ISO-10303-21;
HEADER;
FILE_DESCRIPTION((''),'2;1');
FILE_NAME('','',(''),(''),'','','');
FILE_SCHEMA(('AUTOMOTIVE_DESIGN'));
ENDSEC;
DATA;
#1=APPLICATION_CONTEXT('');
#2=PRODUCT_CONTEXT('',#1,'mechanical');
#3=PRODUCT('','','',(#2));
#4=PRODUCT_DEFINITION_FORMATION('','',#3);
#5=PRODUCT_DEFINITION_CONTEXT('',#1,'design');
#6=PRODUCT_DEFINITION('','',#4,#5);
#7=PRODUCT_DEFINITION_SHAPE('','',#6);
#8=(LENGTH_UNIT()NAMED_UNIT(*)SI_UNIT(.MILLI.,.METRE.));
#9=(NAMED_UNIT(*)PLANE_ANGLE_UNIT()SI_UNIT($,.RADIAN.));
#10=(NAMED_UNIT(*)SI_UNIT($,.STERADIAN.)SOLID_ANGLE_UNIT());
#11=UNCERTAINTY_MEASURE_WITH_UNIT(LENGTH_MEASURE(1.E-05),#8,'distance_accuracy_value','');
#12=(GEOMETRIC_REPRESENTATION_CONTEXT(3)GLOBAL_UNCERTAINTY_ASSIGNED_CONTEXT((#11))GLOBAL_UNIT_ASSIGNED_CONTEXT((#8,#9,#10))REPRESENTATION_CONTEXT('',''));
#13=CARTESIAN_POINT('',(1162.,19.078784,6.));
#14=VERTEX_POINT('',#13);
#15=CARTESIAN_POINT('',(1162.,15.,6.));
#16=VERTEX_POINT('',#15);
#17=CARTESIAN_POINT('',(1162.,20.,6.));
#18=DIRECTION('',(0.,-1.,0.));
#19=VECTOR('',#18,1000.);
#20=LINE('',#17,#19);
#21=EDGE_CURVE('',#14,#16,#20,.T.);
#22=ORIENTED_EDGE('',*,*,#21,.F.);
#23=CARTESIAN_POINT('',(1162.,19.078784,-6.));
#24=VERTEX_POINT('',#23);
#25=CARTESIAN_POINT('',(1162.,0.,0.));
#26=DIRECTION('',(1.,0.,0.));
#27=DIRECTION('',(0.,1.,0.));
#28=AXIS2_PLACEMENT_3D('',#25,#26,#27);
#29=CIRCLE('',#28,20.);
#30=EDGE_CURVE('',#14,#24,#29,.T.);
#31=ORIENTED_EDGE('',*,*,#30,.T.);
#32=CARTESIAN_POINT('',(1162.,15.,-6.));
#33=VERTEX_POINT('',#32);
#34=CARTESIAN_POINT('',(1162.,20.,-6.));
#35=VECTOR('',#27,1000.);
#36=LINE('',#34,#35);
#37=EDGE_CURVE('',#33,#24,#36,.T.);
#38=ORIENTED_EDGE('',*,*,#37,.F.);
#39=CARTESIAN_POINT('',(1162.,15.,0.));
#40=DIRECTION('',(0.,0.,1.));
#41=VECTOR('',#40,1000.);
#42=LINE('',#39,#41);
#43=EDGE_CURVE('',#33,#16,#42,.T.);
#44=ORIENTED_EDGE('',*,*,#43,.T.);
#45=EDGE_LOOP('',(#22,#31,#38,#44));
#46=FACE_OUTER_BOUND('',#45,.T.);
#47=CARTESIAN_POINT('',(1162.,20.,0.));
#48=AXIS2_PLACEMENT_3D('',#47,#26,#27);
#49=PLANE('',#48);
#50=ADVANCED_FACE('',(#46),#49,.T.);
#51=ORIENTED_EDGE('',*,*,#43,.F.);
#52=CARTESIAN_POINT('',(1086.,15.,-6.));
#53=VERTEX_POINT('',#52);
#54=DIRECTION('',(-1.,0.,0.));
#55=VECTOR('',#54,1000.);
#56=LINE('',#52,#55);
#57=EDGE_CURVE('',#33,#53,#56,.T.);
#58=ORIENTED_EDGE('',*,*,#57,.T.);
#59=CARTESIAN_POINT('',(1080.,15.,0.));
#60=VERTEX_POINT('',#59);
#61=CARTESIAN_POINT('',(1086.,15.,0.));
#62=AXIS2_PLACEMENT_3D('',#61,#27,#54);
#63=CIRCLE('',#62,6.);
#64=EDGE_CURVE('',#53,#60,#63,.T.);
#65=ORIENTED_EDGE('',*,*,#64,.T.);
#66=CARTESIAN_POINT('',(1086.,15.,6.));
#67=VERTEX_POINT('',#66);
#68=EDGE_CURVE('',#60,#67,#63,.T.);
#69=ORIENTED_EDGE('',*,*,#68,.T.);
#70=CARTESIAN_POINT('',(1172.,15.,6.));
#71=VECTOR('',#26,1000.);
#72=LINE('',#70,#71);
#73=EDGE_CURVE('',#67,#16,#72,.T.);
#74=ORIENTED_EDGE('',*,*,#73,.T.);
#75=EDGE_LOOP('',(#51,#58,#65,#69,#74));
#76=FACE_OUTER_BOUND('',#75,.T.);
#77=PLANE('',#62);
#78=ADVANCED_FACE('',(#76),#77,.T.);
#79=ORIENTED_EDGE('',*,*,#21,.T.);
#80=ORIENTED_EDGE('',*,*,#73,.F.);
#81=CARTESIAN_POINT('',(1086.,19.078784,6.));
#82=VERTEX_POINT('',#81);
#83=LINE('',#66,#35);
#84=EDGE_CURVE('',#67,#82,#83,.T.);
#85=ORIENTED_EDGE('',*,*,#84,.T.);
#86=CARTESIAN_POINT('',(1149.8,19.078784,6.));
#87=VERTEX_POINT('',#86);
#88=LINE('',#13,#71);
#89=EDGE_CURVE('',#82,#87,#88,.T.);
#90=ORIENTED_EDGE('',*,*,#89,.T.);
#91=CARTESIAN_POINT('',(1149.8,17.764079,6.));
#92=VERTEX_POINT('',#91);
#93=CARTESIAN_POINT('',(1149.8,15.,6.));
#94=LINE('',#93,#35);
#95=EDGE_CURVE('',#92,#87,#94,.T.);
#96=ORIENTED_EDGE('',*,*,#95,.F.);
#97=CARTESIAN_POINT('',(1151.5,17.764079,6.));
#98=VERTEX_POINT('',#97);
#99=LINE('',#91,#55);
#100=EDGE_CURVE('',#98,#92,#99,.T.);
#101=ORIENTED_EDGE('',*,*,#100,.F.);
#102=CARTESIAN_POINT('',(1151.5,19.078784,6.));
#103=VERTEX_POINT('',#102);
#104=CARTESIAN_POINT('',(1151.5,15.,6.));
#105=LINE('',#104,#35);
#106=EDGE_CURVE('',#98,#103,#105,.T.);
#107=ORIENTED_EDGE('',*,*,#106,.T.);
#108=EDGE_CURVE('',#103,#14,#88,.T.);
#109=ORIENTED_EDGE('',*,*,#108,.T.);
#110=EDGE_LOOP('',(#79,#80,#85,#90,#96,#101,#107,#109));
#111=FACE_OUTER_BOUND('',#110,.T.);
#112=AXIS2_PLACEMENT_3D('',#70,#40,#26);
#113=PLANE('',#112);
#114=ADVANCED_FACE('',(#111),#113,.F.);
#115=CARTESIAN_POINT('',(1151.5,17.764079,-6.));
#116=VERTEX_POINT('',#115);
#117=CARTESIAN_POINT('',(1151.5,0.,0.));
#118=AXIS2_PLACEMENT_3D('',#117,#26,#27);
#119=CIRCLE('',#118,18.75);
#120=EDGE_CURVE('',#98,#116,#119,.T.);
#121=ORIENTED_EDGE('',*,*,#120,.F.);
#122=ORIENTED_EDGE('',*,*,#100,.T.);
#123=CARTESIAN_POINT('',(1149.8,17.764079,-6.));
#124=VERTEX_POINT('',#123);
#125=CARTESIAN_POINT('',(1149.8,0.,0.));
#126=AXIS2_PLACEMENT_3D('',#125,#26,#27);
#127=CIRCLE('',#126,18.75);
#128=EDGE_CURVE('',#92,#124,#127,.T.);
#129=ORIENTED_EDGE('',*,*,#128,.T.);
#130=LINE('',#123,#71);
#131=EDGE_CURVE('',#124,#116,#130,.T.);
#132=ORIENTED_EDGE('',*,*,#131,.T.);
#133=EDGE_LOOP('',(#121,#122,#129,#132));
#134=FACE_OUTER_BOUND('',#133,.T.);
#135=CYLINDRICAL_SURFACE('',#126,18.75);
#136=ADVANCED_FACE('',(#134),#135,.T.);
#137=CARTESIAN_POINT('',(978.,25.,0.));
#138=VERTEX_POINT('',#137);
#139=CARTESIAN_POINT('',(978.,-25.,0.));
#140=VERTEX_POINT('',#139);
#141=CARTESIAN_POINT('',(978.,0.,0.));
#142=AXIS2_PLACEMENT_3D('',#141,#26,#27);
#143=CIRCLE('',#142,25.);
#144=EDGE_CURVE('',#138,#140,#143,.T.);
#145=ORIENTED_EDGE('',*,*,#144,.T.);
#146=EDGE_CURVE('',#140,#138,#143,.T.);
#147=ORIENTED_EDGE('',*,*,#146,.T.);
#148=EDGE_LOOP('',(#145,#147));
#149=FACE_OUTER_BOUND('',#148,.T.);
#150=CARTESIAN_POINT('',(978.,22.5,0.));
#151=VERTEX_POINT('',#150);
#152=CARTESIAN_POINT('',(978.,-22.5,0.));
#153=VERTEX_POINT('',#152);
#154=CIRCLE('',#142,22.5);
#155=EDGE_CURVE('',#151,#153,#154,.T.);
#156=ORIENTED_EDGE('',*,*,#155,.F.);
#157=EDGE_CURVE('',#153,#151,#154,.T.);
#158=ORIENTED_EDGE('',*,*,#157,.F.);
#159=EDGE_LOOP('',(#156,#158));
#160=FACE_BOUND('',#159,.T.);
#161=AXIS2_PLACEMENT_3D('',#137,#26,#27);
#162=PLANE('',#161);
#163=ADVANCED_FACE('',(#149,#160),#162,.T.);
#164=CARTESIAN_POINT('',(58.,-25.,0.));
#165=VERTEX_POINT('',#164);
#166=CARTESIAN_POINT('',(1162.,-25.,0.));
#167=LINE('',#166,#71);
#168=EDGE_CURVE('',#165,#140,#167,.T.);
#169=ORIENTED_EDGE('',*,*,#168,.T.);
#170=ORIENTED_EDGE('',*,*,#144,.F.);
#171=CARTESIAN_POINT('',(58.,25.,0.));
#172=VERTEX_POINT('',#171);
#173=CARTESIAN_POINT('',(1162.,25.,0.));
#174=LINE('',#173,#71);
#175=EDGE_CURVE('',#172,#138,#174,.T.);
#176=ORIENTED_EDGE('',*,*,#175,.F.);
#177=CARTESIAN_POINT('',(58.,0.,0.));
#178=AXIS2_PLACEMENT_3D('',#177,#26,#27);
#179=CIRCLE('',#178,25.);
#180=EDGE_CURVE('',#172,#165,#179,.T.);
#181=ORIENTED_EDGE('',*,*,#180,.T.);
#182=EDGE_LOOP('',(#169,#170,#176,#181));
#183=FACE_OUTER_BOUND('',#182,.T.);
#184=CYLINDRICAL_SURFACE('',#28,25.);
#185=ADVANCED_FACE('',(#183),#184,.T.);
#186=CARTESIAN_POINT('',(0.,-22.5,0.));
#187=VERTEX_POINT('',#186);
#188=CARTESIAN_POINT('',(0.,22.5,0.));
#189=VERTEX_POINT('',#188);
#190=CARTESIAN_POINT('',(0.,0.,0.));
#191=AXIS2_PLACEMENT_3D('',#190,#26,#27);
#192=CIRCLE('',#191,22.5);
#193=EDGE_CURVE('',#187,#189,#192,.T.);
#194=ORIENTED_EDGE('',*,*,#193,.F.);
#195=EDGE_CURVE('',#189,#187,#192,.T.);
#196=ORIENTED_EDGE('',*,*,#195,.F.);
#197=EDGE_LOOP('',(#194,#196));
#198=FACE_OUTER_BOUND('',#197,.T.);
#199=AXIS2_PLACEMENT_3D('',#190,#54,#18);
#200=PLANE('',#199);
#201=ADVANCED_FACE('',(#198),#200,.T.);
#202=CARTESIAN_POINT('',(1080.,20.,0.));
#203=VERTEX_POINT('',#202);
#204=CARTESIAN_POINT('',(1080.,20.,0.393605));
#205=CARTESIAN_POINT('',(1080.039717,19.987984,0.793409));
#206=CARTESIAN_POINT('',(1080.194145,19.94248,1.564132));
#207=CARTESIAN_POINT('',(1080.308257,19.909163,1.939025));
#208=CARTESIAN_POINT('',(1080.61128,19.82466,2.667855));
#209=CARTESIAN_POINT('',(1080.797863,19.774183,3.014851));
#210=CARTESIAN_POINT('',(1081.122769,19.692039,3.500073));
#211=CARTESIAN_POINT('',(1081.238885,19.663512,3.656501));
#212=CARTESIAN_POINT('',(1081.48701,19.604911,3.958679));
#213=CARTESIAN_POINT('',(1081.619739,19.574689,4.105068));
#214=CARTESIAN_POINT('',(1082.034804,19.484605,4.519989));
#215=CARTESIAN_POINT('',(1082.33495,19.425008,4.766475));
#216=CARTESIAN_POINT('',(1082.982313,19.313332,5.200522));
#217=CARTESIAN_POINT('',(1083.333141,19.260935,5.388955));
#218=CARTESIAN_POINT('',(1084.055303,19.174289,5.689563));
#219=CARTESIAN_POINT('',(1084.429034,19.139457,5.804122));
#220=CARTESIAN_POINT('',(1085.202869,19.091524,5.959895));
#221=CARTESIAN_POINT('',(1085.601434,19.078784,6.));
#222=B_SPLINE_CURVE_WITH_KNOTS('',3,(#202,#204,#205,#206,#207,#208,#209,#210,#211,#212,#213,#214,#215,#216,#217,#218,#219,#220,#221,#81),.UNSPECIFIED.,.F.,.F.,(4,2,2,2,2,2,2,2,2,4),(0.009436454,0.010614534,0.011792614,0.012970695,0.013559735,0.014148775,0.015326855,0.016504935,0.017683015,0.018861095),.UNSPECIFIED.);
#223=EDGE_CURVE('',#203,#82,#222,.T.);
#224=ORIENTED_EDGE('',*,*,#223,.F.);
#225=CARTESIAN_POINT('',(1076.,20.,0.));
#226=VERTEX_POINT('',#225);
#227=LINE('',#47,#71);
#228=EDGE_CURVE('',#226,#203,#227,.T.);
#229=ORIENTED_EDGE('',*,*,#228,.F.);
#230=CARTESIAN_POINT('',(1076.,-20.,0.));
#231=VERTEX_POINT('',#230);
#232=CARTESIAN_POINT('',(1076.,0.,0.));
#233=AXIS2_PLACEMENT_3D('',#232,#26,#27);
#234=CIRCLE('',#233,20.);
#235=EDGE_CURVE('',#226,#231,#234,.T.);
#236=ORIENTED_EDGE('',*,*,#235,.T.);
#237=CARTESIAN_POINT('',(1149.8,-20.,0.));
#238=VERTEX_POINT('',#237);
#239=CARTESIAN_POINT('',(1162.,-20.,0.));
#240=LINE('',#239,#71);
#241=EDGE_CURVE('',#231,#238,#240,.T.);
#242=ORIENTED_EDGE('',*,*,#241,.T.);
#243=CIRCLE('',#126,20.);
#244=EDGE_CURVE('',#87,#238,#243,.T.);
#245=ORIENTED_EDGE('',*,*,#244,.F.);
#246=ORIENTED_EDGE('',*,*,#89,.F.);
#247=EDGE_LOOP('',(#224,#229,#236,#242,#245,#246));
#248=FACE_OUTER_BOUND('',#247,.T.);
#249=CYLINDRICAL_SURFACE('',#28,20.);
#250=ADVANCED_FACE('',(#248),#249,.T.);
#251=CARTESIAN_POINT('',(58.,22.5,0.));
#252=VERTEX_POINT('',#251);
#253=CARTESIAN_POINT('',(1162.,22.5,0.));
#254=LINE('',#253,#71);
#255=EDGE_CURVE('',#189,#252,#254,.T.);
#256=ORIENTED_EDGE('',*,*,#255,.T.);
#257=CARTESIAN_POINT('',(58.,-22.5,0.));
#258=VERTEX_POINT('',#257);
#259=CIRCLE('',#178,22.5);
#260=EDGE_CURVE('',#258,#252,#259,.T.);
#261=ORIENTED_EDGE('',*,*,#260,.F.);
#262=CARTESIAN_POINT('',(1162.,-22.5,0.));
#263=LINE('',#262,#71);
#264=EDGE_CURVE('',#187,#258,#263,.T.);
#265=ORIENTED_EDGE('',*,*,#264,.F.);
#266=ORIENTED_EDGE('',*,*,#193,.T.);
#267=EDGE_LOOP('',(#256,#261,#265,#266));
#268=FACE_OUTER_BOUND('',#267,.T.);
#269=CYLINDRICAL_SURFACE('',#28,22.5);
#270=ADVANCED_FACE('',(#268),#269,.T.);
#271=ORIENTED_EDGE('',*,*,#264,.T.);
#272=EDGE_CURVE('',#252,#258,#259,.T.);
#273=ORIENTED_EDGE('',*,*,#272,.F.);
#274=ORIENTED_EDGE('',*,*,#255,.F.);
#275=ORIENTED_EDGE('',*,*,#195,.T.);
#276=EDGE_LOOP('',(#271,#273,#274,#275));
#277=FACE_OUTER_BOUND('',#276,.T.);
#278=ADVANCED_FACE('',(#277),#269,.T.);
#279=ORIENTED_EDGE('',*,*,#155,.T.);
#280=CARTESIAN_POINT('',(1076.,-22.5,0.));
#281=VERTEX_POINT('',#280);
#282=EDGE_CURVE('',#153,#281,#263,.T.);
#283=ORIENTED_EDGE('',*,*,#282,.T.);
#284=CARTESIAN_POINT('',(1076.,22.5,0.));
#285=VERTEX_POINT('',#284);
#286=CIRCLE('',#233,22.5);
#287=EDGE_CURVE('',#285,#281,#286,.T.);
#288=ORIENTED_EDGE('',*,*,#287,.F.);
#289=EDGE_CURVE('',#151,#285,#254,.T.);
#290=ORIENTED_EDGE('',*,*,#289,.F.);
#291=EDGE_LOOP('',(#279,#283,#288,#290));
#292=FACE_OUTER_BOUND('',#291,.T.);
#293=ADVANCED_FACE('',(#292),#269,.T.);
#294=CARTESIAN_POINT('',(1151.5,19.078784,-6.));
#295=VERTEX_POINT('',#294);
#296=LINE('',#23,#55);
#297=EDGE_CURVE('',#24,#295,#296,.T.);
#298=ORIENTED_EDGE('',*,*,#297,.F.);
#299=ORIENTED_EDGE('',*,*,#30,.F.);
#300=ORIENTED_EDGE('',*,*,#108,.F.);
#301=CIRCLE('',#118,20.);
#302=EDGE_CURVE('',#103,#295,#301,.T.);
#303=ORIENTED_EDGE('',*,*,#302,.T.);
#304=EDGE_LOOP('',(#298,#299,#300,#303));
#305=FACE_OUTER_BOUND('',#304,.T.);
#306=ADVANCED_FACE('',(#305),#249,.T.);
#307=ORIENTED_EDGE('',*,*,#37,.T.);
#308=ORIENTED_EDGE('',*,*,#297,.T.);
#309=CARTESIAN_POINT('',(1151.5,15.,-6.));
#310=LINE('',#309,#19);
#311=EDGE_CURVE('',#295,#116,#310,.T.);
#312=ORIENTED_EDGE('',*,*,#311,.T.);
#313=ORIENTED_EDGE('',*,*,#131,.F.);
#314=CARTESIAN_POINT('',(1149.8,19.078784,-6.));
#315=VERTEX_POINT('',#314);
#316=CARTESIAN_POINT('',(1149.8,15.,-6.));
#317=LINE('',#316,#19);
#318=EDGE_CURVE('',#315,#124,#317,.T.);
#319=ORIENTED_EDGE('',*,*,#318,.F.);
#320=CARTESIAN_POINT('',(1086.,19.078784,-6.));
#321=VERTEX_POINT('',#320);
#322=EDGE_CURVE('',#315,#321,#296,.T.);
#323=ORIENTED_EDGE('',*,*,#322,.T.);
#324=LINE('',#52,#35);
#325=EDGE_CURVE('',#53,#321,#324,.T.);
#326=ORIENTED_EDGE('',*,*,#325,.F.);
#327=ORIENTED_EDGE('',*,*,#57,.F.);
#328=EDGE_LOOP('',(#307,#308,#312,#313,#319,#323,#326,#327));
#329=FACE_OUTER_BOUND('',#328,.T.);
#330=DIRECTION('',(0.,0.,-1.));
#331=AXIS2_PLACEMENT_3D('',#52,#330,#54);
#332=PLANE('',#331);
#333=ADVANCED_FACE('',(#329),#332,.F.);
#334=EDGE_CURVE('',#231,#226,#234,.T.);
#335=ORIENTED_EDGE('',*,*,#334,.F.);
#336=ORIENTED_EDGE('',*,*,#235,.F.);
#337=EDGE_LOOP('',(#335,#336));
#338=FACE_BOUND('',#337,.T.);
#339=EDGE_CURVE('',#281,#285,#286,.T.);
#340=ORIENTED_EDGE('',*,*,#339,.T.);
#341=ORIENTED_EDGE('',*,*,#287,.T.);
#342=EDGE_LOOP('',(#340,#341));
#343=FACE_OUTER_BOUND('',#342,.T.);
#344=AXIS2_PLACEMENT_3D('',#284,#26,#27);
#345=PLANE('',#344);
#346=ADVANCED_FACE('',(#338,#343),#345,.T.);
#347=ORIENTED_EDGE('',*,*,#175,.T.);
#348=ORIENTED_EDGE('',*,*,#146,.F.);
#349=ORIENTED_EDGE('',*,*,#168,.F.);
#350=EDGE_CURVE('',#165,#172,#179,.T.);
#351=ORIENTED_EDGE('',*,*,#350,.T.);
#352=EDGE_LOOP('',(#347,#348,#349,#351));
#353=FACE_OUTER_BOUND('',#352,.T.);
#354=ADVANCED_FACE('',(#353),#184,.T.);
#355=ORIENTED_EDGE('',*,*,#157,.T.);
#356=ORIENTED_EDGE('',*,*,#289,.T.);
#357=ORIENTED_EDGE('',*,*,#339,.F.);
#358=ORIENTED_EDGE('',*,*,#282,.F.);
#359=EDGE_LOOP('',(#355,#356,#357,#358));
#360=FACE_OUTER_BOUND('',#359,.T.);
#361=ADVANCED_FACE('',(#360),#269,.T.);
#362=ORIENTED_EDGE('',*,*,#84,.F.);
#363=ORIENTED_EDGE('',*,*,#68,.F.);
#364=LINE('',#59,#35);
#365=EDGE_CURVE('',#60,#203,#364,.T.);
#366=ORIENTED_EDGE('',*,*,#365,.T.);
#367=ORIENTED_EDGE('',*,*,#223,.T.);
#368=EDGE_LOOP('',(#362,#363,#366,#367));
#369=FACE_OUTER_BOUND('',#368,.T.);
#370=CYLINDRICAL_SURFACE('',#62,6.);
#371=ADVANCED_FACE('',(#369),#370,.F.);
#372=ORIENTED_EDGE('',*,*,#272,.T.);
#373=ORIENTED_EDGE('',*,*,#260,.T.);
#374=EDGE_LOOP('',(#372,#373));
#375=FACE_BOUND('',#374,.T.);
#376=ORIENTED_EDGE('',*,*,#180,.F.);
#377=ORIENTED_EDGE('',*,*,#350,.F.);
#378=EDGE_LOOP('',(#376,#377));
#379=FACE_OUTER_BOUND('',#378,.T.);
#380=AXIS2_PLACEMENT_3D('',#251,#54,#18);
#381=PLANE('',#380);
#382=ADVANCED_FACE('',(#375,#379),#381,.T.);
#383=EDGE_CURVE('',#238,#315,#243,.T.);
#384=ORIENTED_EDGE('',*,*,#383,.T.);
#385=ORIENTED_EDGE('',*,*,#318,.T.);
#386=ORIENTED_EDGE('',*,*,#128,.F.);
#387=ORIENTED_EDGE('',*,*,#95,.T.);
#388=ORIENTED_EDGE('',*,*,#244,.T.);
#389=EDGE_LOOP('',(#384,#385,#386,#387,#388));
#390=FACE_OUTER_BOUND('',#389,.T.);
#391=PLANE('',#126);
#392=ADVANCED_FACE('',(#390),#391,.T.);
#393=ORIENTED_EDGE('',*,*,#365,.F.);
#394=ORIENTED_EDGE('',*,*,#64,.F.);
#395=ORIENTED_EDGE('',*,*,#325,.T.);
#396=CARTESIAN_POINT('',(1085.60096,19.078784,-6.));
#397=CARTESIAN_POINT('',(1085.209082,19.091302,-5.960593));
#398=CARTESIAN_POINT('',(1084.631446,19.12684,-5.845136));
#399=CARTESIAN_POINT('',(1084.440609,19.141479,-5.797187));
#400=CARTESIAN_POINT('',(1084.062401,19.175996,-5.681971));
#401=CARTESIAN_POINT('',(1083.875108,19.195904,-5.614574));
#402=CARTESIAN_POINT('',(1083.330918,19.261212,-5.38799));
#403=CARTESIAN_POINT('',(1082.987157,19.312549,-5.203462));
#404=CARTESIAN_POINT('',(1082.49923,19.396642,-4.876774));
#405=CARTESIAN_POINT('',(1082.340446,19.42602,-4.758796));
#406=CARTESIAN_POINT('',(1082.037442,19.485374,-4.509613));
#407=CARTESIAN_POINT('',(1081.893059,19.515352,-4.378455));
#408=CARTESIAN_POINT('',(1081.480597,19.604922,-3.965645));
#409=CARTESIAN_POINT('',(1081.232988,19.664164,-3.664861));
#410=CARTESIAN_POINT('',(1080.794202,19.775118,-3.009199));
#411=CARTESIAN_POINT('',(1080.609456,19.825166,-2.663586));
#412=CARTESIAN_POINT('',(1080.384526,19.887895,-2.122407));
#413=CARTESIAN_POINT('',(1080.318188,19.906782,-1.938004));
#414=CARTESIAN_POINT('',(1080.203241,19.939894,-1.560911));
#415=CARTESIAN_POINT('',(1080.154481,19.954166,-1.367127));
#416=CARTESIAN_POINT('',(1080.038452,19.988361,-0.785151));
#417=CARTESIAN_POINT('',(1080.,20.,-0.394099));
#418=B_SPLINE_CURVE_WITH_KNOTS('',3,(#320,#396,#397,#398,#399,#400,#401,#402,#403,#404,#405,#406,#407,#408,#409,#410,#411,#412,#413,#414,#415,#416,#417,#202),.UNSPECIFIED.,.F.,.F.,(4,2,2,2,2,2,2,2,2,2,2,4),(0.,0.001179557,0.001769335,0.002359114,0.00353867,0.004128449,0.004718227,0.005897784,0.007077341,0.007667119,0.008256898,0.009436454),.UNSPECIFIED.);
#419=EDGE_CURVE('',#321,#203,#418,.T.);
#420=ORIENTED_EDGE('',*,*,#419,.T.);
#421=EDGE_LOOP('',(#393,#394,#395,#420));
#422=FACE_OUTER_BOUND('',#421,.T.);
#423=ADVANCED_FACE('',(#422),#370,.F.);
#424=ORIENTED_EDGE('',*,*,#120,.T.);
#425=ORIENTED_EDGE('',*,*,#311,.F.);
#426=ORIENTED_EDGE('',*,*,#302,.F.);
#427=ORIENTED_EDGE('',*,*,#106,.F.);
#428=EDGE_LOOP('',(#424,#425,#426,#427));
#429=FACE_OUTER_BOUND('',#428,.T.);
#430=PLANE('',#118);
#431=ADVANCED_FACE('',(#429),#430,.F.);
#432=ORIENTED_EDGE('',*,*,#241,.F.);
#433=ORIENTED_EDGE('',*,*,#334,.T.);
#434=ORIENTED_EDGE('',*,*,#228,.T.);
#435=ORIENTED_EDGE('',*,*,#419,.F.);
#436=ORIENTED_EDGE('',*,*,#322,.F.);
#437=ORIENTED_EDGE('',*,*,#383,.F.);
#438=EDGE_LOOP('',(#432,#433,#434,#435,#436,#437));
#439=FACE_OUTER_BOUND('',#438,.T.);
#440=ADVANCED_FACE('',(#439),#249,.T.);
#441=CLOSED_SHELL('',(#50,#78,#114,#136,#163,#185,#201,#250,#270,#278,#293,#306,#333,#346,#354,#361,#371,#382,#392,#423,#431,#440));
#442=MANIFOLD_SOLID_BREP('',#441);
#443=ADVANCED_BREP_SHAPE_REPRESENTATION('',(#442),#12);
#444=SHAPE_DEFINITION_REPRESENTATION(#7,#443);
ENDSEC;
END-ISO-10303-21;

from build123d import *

# Parameters (mm, degrees)
CUT_EXTRUDE_1_DEPTH = 5
SKETCH_3_R          = 20
SKETCH_3_R_2        = 18.75
CUT_EXTRUDE_2_DEPTH = 1.7


with BuildPart() as part:
    # 草图1 → 旋转1 (revolve)
    with BuildSketch(Plane.XY):
        Polygon((0, 0), (0, 22.5), (58, 22.5), (58, 25), (978, 25), (978, 22.5), (1076, 22.5), (1076, 20), (1162, 20), (1162, 0), align=None)
    revolve(axis=Axis((1162, 0, 0), (-1, 0, 0)))

    # 草图2 → 切除-拉伸1 (cut)
    with BuildSketch(Plane(origin=(0, 20, 0), x_dir=(1, 0, 0), z_dir=(0, 1, 0))):
        with BuildLine():
            Line((1086, 6), (1172, 6))
            Line((1172, 6), (1172, -6))
            Line((1172, -6), (1086, -6))
            ThreePointArc((1086, -6), (1080, 0), (1086, 6))
        make_face()
    extrude(amount=-CUT_EXTRUDE_1_DEPTH, mode=Mode.SUBTRACT)

    # 草图3 → 切除-拉伸2 (cut)
    with BuildSketch(Plane(origin=(1151.5, 0, 0), x_dir=(0, 0, -1), z_dir=(1, 0, 0))):
        with Locations(Location((0, 0, 0), (0, 0, 90))):
            Circle(SKETCH_3_R)
        Circle(SKETCH_3_R_2, mode=Mode.SUBTRACT)
    extrude(amount=-CUT_EXTRUDE_2_DEPTH, mode=Mode.SUBTRACT)


solid = part.part
